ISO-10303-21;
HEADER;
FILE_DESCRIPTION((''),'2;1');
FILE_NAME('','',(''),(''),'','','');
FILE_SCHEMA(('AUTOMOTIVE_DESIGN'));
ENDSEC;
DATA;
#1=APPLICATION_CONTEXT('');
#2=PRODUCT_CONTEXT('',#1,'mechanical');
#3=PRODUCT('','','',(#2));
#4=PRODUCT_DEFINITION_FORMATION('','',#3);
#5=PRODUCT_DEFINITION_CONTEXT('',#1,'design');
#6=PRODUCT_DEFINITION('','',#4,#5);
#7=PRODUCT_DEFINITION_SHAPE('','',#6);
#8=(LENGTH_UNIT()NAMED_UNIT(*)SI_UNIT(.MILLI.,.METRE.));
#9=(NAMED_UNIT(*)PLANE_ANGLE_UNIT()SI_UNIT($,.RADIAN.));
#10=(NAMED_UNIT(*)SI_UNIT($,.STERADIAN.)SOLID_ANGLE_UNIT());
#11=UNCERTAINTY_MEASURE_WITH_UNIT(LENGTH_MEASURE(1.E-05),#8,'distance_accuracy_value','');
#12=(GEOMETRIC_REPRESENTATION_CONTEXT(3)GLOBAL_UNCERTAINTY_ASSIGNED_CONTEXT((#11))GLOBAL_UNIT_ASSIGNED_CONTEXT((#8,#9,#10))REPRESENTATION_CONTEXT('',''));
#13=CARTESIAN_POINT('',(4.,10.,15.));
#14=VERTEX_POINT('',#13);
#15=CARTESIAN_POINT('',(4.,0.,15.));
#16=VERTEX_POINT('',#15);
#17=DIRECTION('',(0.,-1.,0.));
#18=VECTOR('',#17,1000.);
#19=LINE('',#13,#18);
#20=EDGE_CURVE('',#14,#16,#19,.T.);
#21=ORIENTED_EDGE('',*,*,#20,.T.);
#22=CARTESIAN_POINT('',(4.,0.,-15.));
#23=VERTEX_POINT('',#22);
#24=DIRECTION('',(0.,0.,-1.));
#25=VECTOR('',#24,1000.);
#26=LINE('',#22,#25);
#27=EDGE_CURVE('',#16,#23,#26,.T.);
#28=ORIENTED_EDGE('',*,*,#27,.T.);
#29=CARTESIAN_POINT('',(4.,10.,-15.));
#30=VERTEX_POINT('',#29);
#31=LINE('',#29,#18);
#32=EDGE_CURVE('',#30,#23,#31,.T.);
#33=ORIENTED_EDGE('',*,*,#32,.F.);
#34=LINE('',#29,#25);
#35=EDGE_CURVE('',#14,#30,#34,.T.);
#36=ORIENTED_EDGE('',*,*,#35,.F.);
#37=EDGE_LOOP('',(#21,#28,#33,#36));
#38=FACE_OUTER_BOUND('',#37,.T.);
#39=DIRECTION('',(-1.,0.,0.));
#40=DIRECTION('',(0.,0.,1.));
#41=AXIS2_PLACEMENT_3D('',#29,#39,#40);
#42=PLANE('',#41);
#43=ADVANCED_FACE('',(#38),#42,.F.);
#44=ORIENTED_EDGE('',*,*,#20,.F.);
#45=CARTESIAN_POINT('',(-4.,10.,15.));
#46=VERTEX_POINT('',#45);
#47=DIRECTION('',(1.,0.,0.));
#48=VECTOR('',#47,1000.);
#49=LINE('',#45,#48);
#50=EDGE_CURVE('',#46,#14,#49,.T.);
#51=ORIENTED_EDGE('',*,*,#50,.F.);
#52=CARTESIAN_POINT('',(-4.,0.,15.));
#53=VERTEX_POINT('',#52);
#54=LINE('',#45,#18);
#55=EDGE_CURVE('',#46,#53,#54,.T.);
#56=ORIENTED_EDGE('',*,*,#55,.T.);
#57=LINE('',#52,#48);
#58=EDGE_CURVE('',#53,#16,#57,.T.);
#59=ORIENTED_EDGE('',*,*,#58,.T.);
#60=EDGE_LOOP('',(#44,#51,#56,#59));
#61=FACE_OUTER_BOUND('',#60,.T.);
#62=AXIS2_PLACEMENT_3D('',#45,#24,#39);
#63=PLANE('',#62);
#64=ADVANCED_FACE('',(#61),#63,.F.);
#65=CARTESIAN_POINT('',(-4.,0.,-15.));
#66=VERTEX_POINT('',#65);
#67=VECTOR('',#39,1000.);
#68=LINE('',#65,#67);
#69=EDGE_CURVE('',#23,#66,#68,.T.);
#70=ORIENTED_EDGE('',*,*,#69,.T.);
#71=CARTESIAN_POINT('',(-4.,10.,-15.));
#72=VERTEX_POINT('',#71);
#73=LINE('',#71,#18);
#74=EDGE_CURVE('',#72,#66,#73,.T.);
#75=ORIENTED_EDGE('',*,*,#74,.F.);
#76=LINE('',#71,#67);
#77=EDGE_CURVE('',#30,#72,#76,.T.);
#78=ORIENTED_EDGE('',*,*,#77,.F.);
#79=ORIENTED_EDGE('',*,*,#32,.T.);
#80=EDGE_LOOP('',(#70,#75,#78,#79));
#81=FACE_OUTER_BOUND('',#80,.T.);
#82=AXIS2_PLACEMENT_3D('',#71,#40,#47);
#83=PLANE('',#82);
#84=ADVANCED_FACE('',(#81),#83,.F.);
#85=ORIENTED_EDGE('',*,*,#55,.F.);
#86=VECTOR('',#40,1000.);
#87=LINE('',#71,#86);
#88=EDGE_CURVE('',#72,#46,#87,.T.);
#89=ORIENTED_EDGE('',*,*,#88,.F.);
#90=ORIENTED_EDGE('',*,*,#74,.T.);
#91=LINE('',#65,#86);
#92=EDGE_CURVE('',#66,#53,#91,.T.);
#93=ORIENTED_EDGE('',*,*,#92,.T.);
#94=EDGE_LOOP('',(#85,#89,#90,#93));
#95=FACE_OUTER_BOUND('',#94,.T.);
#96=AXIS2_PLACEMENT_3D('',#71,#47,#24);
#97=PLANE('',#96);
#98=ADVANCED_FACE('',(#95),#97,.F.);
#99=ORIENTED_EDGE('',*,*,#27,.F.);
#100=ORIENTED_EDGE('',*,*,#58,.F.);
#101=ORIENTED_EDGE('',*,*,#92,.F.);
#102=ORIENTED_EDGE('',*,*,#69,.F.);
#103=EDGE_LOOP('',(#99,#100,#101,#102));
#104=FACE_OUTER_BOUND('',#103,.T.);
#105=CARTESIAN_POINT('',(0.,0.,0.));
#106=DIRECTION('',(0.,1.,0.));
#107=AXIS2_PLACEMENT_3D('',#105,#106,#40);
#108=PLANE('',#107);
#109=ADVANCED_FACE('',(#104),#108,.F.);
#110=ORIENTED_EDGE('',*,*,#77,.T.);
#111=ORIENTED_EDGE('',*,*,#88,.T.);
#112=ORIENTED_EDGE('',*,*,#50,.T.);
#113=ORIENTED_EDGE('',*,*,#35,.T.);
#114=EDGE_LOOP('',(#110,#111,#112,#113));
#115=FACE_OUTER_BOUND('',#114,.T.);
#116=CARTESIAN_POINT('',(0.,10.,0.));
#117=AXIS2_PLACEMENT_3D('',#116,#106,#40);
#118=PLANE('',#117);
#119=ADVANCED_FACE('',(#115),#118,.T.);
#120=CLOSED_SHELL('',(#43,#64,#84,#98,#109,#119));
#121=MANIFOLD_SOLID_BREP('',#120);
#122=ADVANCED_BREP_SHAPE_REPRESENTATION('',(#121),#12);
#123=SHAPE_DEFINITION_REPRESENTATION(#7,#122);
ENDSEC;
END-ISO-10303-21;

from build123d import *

# Parameters (mm, degrees)
SKETCH1_W           = 8
SKETCH1_H           = 30
BOSS_EXTRUDE1_DEPTH = 10


with BuildPart() as part:
    # Sketch1 → Boss-Extrude1 (new body)
    with BuildSketch(Plane(origin=(0, 0, 0), x_dir=(1, 0, 0), z_dir=(0, 1, 0))):
        Rectangle(SKETCH1_W, SKETCH1_H)
    extrude(amount=BOSS_EXTRUDE1_DEPTH)


solid = part.part
